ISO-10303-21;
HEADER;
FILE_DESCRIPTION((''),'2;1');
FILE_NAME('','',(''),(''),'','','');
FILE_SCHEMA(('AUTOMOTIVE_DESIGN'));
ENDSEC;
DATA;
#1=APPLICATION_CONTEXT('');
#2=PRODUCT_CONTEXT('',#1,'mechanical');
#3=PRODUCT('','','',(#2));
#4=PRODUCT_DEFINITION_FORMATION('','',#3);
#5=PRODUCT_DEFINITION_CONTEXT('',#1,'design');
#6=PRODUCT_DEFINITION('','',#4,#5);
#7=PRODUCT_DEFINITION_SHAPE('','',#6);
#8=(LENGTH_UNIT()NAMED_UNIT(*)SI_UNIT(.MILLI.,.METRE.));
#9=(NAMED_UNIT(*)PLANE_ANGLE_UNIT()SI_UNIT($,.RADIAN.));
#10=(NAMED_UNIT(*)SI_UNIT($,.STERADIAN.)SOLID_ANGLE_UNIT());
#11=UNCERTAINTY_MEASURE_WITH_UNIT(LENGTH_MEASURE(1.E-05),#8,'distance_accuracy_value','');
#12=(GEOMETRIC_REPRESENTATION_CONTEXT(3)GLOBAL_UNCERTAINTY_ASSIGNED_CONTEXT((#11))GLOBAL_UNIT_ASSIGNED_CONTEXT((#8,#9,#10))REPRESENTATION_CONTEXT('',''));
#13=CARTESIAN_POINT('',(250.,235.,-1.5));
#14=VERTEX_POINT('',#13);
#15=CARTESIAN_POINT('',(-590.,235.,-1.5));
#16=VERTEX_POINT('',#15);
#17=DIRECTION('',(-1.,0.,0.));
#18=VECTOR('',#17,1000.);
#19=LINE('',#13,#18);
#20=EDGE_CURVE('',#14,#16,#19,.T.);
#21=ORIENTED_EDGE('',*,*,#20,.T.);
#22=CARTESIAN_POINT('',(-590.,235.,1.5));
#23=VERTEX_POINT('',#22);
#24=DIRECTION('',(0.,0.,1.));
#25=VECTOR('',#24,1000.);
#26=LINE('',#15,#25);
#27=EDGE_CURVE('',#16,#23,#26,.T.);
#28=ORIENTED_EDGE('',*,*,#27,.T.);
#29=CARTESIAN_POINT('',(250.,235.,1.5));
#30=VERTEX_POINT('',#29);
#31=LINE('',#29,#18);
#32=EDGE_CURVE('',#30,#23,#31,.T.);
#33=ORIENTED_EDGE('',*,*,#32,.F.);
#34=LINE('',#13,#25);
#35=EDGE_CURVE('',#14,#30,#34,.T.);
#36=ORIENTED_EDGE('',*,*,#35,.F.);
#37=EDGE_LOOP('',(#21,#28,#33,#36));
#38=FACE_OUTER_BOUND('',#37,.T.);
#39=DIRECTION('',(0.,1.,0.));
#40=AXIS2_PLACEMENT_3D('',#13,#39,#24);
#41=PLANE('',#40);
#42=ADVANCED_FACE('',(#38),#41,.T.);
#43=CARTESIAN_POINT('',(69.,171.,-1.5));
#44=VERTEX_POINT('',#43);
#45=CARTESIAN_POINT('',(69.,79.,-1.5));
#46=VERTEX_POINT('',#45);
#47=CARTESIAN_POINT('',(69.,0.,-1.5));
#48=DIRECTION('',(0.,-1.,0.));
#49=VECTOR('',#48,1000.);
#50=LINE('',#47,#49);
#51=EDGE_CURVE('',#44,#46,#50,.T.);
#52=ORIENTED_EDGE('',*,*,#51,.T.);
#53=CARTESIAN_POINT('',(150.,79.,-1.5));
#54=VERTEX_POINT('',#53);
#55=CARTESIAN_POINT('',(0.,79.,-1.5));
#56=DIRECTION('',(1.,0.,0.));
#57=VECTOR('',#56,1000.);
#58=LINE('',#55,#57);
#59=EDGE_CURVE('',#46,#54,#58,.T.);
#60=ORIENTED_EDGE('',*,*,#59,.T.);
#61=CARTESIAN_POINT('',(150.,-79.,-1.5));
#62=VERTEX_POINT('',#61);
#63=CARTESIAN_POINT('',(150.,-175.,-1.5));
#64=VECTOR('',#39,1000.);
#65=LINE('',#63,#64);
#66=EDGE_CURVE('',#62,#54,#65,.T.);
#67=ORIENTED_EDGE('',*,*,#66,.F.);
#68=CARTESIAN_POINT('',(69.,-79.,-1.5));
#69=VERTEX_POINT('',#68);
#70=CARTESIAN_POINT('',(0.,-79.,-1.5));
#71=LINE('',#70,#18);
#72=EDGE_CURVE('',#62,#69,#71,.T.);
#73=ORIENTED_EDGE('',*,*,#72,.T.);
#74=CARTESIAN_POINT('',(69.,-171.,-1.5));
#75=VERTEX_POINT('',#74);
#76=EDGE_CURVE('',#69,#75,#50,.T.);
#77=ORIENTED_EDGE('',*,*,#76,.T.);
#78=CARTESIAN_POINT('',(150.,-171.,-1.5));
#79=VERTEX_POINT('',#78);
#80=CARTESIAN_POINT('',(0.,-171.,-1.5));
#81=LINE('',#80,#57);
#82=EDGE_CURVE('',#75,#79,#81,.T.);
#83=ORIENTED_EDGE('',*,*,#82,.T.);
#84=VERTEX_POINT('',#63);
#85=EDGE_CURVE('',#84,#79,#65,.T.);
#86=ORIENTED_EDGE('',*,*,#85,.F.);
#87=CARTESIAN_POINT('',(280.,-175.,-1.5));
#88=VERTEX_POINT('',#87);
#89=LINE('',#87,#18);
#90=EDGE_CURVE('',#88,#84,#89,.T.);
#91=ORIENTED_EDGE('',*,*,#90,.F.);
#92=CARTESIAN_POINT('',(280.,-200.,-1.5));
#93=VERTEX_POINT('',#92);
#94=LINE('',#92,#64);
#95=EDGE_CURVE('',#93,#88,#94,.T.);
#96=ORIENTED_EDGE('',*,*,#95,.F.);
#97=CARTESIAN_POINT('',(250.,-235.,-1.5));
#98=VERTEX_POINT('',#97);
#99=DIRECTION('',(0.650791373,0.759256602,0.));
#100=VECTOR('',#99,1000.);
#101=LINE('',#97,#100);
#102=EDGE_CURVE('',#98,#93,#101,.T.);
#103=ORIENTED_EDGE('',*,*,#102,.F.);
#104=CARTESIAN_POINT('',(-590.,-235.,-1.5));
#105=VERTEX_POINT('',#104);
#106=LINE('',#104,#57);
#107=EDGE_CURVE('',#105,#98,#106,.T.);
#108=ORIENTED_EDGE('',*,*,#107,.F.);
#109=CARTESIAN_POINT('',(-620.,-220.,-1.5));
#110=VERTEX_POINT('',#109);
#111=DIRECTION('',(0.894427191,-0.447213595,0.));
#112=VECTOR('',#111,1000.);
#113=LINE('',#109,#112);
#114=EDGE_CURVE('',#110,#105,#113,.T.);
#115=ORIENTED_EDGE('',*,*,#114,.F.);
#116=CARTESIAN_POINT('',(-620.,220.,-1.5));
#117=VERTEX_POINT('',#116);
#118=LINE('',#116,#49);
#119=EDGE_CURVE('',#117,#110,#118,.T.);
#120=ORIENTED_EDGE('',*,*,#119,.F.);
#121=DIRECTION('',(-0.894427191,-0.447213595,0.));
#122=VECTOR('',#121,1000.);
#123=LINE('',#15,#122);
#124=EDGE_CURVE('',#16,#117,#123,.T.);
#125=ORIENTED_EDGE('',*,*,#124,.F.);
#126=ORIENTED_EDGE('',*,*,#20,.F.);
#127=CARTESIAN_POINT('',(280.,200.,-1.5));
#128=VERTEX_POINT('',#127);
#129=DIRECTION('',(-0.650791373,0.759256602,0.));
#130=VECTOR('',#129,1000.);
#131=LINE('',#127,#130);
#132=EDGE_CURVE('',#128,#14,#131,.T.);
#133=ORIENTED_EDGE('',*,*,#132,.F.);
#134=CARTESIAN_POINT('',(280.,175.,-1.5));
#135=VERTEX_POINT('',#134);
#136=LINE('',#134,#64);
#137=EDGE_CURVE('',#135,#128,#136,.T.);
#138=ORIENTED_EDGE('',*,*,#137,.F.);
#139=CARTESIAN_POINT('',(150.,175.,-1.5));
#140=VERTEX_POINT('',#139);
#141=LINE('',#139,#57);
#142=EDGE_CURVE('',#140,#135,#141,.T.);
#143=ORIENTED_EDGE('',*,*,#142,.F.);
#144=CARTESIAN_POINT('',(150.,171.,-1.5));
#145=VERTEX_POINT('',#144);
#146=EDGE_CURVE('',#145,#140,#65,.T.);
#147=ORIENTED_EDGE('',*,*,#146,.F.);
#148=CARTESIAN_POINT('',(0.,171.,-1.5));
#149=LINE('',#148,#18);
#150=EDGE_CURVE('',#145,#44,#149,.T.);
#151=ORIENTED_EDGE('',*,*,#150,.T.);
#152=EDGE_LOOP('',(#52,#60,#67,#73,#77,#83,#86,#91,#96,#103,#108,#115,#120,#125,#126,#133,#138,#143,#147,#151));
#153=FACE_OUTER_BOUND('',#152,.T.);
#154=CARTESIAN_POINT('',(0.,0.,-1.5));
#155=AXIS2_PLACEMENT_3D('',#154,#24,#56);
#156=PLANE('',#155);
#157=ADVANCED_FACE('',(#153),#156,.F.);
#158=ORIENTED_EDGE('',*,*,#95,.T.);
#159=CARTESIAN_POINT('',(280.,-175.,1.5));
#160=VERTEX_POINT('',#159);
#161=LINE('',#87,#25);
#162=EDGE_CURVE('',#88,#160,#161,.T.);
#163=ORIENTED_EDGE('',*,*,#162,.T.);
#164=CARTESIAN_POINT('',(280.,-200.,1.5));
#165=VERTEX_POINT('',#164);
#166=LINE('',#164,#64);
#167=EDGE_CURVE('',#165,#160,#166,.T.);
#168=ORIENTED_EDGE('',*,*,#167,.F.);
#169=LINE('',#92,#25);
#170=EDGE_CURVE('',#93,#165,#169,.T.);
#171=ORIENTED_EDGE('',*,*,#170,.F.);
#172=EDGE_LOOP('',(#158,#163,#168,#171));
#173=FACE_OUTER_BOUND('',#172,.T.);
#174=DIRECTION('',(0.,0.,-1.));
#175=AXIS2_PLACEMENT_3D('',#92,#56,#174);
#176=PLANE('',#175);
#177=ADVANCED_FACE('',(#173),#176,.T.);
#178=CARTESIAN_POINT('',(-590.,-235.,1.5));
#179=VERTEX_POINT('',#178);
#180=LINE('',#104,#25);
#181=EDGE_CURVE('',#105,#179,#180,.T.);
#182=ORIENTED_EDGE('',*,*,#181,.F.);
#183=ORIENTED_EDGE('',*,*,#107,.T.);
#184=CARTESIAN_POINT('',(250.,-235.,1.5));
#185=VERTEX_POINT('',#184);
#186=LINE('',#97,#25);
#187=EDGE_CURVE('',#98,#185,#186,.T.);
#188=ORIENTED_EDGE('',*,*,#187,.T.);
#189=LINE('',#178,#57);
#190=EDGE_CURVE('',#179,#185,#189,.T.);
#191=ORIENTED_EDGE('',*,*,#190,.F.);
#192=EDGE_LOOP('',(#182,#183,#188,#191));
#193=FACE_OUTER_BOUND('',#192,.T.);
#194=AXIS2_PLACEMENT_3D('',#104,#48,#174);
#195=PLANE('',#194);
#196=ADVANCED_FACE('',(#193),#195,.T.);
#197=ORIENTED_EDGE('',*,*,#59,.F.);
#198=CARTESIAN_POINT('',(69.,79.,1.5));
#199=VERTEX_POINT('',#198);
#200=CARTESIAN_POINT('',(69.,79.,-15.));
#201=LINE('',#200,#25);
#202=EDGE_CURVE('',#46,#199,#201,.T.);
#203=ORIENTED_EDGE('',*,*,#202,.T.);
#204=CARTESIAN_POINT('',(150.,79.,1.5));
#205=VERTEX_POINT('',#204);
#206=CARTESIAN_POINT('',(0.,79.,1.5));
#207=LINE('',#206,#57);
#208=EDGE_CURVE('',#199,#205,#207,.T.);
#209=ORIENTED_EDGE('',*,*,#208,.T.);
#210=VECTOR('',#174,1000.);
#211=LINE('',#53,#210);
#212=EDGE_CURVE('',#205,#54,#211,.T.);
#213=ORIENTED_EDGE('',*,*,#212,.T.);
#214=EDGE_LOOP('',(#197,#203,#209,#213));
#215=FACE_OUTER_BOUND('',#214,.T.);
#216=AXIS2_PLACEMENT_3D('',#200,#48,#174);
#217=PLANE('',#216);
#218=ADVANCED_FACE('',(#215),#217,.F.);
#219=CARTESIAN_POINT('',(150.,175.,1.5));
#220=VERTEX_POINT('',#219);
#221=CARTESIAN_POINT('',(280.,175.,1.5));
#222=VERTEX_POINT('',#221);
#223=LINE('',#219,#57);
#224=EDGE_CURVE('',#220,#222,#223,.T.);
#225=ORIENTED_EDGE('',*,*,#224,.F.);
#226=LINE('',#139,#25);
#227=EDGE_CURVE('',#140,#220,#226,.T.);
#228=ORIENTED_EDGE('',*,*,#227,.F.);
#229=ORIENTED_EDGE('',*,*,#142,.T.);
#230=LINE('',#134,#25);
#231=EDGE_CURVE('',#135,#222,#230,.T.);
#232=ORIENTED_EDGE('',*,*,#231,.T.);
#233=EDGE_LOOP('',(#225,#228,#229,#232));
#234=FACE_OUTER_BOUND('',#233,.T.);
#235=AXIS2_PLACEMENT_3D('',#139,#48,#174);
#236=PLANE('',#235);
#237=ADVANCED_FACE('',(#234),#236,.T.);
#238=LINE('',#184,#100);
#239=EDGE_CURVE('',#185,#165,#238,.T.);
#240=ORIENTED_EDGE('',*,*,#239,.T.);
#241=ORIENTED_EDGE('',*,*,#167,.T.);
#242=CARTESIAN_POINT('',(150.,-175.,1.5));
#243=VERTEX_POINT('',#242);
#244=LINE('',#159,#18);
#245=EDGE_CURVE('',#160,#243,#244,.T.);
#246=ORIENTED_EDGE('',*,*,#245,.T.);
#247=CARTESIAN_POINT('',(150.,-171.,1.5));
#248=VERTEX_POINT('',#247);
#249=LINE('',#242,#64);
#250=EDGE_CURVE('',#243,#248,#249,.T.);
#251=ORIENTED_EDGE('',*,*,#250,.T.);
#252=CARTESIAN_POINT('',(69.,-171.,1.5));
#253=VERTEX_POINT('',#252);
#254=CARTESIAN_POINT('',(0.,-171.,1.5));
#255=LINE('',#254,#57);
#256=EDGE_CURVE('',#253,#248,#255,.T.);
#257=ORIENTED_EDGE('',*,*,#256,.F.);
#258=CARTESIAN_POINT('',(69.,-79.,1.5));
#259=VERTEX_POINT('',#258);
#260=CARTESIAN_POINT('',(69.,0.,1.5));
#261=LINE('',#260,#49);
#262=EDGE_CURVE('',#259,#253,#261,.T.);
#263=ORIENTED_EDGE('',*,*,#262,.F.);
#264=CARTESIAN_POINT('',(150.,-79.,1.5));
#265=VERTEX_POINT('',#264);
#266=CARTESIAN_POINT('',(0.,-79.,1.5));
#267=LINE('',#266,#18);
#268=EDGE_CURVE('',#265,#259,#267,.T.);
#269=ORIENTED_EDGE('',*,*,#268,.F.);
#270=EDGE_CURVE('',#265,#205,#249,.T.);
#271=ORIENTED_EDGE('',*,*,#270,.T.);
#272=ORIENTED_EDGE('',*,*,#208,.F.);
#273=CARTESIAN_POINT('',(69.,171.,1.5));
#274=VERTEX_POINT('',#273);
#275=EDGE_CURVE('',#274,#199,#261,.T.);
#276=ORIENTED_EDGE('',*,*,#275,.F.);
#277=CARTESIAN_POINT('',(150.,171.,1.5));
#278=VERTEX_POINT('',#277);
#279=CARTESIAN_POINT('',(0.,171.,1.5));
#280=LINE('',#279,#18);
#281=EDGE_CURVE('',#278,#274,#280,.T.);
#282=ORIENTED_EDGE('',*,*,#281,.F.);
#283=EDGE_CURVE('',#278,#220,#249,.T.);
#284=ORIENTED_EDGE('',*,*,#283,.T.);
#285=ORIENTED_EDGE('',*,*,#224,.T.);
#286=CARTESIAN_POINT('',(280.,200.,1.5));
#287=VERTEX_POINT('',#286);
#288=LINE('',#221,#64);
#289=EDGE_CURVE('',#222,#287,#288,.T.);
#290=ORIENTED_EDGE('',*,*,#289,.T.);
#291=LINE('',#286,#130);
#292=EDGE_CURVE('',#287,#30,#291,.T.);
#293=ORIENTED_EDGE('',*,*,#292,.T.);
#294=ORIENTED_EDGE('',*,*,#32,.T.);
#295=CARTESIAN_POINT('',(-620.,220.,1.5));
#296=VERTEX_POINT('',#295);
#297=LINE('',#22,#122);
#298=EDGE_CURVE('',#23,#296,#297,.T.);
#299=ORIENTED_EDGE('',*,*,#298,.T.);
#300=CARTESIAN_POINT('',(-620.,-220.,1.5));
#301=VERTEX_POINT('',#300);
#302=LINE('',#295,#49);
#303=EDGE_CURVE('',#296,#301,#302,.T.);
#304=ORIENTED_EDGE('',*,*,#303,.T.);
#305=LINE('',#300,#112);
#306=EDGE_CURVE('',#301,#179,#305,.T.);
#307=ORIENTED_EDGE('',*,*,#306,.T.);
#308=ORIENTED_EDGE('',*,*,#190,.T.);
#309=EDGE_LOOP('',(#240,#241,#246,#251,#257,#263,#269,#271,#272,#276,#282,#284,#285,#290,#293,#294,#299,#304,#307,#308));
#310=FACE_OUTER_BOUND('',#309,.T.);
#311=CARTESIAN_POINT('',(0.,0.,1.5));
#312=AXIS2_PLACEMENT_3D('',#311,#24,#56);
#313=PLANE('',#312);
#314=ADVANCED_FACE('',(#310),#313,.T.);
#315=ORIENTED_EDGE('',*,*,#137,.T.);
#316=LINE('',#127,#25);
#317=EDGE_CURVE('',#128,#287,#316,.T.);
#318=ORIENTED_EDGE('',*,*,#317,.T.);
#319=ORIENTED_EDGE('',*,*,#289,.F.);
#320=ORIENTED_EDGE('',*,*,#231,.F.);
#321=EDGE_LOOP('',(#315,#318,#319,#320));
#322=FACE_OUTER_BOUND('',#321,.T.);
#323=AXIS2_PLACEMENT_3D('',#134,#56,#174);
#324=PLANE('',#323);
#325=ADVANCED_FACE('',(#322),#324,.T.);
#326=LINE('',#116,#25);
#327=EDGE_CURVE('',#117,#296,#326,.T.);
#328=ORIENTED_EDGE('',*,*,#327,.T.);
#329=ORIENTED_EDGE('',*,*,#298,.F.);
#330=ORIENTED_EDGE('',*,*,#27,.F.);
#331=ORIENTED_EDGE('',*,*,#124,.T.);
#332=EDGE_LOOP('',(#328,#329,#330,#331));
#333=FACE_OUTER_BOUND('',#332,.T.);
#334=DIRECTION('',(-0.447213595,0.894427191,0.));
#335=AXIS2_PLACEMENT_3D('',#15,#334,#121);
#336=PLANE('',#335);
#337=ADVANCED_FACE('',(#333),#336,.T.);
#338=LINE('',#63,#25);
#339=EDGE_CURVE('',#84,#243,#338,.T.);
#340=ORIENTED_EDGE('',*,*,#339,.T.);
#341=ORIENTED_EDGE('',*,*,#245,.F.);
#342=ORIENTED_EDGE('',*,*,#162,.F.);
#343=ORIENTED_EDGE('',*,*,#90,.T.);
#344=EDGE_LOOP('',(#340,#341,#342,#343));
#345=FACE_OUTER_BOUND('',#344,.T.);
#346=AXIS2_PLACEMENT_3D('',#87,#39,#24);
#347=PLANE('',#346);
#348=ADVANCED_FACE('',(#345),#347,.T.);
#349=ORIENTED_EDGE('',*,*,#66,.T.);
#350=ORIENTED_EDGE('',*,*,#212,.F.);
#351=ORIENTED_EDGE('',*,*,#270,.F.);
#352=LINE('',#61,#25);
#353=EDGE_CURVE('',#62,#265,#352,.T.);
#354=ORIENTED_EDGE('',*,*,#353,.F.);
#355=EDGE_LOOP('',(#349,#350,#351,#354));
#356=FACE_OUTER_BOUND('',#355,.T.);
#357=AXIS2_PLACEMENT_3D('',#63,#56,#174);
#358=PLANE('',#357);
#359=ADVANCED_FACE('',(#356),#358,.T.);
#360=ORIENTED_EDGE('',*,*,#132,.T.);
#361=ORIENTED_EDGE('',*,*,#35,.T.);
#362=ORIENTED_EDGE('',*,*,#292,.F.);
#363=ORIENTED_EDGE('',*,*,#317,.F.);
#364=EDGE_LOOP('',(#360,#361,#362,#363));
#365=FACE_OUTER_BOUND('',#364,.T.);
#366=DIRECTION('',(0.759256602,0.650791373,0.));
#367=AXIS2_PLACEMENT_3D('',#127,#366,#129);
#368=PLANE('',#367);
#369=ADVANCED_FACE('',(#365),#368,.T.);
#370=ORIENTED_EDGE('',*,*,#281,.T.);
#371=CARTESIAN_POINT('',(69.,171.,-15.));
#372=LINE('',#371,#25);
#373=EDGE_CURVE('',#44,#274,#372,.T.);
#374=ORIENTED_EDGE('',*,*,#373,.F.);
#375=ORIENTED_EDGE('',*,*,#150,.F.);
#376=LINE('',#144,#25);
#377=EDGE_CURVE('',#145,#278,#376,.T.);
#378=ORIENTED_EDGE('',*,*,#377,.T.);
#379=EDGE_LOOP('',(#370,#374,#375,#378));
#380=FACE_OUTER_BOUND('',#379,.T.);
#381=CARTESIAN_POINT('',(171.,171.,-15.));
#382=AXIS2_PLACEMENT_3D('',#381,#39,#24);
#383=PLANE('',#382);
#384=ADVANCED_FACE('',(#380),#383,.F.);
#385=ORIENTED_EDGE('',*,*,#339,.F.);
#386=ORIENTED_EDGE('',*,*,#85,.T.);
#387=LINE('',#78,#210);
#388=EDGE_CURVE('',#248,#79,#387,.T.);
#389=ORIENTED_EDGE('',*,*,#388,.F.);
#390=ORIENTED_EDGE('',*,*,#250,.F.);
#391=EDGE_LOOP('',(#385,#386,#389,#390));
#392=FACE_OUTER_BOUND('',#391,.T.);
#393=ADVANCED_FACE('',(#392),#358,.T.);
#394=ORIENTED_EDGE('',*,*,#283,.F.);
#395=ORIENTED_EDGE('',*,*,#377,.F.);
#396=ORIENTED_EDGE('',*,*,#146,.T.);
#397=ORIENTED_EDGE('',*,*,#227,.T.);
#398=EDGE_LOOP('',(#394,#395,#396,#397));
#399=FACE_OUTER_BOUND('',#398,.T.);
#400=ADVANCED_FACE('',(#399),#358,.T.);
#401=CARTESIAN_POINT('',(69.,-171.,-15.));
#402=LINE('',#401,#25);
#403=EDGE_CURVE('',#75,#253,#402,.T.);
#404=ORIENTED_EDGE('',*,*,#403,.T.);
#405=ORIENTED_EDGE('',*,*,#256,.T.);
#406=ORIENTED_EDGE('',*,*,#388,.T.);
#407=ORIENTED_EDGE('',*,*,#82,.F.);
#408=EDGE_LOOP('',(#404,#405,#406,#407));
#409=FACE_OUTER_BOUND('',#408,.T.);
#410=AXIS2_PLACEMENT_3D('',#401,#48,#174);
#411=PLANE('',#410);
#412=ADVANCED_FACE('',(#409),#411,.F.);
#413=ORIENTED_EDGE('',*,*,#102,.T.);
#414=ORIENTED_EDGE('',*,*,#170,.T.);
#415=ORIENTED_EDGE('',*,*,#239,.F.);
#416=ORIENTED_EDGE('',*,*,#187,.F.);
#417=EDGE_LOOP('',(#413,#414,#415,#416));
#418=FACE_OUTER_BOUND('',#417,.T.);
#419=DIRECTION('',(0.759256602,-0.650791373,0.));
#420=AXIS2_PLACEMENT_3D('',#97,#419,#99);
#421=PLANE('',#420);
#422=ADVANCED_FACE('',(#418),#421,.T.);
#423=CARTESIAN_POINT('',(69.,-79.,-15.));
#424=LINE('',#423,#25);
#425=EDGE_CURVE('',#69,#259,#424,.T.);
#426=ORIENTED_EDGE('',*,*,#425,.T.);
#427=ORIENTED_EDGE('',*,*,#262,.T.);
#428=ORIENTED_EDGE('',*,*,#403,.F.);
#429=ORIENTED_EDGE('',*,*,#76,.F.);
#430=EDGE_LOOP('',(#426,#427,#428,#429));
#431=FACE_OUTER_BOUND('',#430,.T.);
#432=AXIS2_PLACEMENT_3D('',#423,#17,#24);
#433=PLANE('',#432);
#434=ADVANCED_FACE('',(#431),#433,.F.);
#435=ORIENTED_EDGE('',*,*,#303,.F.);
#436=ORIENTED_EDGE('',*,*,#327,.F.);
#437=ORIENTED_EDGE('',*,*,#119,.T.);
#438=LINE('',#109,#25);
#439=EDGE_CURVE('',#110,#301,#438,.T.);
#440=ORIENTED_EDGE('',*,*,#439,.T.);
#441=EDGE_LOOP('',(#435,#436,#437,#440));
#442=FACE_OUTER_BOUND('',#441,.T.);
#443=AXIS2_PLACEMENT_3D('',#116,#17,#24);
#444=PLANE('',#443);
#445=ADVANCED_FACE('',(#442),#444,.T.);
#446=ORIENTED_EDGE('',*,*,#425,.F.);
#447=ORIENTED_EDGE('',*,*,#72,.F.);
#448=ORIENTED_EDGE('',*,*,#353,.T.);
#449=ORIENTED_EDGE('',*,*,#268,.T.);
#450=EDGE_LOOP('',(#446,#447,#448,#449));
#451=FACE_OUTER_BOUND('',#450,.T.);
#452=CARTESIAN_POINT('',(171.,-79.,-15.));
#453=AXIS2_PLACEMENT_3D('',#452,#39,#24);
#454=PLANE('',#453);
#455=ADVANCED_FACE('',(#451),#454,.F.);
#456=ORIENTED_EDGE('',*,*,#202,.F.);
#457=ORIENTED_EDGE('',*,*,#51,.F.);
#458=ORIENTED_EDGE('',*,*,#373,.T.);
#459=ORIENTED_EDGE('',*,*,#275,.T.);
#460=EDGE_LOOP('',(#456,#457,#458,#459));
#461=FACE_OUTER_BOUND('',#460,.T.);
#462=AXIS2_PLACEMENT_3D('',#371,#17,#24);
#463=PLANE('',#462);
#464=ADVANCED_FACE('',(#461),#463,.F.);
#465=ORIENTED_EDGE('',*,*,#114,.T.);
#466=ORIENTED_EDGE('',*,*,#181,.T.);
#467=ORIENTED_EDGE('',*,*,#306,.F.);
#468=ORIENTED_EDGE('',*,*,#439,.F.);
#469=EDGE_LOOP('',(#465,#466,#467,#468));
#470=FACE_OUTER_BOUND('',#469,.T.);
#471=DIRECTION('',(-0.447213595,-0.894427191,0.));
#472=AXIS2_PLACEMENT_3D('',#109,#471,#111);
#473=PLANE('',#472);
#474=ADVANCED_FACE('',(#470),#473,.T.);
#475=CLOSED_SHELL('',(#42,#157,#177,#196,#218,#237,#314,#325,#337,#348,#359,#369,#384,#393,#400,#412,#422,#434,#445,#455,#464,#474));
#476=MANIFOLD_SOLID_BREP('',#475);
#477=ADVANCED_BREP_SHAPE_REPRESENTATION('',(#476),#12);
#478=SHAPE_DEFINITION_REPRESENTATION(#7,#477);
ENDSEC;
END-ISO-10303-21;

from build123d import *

# Parameters (mm, degrees)
EXTRUDE_1_DEPTH     = 1.5
SKETCH_2_W          = 102
SKETCH_2_H          = 92
CUT_EXTRUDE_1_DEPTH = 15


with BuildPart() as part:
    # 草图1 → 凸台-拉伸1 (new, symmetric)
    with BuildSketch(Plane.XY):
        Polygon((-620, -220), (-590, -235), (250, -235), (280, -200), (280, -175), (150, -175), (150, 175), (280, 175), (280, 200), (250, 235), (-590, 235), (-620, 220), align=None)
    extrude(amount=EXTRUDE_1_DEPTH, both=True)

    # 草图2 → 切除-拉伸1 (cut, symmetric)
    with BuildSketch(Plane.XY):
        with Locations((120, 125)):
            Rectangle(SKETCH_2_W, SKETCH_2_H)
        with Locations((120, -125)):
            Rectangle(SKETCH_2_W, SKETCH_2_H)
    extrude(amount=CUT_EXTRUDE_1_DEPTH, both=True, mode=Mode.SUBTRACT)


solid = part.part
